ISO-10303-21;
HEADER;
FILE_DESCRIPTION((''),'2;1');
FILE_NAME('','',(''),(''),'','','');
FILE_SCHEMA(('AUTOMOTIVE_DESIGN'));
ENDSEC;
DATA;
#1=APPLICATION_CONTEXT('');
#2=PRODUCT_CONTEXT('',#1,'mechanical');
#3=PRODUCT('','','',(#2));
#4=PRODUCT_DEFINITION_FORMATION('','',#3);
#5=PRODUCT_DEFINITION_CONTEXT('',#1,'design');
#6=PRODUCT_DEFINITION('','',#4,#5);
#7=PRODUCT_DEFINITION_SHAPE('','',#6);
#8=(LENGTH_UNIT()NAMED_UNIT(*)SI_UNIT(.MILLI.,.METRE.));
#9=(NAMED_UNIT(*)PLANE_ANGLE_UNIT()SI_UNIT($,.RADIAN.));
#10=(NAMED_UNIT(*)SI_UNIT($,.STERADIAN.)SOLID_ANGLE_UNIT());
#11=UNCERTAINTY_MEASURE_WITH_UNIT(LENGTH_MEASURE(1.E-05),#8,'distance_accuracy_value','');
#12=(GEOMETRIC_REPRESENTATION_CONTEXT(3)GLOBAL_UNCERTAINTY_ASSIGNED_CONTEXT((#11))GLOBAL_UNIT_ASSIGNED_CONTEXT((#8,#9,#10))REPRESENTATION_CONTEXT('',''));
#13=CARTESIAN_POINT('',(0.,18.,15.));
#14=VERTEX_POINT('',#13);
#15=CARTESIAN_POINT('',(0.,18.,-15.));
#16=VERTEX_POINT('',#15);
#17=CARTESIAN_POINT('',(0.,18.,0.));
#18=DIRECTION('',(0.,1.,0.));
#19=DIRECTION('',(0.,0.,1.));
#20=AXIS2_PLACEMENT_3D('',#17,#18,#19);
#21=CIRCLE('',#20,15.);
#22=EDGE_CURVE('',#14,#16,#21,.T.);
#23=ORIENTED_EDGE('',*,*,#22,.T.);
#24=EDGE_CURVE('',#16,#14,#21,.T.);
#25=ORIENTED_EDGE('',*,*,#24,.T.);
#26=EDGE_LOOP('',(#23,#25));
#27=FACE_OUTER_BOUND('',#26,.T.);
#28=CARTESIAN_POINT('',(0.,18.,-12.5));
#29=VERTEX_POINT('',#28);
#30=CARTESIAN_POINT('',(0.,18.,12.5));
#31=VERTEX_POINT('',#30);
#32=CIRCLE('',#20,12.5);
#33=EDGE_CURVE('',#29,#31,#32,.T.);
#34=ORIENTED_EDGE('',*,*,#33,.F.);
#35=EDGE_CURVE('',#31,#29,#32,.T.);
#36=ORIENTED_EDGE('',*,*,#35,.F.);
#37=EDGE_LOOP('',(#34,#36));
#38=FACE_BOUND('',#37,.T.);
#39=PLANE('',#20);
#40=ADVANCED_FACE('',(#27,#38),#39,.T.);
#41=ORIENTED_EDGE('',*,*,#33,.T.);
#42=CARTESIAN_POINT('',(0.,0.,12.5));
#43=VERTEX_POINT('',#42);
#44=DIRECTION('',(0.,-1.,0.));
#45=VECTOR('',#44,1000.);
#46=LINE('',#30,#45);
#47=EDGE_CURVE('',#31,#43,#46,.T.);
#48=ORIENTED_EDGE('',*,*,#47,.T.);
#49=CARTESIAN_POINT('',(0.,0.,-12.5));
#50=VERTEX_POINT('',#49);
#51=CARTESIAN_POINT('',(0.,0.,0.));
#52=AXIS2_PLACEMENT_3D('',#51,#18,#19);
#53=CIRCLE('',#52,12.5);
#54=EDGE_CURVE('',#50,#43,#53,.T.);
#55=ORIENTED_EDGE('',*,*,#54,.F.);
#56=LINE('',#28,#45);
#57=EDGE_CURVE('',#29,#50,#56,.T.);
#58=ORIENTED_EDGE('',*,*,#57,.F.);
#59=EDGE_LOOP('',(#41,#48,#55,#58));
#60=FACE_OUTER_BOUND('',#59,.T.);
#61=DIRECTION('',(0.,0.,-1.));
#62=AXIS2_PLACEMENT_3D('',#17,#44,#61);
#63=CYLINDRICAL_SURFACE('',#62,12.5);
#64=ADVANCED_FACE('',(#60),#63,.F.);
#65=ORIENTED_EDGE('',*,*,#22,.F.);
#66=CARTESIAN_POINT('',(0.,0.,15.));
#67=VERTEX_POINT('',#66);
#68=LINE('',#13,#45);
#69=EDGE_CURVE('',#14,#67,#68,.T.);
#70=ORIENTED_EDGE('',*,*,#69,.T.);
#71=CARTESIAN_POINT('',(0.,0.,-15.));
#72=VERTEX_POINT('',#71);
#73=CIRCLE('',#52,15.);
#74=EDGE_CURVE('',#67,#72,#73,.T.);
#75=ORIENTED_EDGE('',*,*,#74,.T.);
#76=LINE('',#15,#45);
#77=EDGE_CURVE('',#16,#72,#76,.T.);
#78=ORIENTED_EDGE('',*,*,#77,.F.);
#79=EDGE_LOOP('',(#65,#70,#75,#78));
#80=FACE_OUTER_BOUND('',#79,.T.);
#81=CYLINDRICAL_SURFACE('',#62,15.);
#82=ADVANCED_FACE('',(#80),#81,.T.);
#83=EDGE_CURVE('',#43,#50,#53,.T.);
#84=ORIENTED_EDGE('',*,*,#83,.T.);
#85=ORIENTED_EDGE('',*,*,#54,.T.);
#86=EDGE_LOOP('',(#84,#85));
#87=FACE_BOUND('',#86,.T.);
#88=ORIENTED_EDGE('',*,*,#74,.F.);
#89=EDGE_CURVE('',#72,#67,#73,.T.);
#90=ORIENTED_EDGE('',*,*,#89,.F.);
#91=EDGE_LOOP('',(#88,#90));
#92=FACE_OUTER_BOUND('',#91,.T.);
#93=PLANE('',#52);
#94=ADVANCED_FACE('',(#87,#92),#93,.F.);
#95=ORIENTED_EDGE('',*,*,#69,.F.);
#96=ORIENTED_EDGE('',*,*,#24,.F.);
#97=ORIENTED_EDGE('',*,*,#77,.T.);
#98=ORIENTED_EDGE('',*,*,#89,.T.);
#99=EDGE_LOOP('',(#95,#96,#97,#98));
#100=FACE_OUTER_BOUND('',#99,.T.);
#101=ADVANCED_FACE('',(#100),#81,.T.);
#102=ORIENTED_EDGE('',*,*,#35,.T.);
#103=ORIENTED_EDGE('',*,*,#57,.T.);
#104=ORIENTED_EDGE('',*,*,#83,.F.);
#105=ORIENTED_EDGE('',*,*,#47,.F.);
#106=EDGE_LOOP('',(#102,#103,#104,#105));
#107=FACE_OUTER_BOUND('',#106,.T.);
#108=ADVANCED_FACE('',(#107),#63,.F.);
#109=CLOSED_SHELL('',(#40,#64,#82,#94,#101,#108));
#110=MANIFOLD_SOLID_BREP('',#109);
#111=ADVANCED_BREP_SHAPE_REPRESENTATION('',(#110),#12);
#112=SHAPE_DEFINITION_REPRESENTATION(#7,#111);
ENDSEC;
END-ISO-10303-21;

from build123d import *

# Parameters (mm, degrees)
SKETCH1_R           = 15
SKETCH1_R_2         = 12.5
BOSS_EXTRUDE1_DEPTH = 18


with BuildPart() as part:
    # Sketch1 → Boss-Extrude1 (new body)
    with BuildSketch(Plane(origin=(0, 0, 0), x_dir=(1, 0, 0), z_dir=(0, 1, 0))):
        with Locations(Location((0, 0, 0), (0, 0, 270))):
            Circle(SKETCH1_R)
        with Locations(Location((0, 0, 0), (0, 0, 270))):
            Circle(SKETCH1_R_2, mode=Mode.SUBTRACT)
    extrude(amount=BOSS_EXTRUDE1_DEPTH)


solid = part.part
